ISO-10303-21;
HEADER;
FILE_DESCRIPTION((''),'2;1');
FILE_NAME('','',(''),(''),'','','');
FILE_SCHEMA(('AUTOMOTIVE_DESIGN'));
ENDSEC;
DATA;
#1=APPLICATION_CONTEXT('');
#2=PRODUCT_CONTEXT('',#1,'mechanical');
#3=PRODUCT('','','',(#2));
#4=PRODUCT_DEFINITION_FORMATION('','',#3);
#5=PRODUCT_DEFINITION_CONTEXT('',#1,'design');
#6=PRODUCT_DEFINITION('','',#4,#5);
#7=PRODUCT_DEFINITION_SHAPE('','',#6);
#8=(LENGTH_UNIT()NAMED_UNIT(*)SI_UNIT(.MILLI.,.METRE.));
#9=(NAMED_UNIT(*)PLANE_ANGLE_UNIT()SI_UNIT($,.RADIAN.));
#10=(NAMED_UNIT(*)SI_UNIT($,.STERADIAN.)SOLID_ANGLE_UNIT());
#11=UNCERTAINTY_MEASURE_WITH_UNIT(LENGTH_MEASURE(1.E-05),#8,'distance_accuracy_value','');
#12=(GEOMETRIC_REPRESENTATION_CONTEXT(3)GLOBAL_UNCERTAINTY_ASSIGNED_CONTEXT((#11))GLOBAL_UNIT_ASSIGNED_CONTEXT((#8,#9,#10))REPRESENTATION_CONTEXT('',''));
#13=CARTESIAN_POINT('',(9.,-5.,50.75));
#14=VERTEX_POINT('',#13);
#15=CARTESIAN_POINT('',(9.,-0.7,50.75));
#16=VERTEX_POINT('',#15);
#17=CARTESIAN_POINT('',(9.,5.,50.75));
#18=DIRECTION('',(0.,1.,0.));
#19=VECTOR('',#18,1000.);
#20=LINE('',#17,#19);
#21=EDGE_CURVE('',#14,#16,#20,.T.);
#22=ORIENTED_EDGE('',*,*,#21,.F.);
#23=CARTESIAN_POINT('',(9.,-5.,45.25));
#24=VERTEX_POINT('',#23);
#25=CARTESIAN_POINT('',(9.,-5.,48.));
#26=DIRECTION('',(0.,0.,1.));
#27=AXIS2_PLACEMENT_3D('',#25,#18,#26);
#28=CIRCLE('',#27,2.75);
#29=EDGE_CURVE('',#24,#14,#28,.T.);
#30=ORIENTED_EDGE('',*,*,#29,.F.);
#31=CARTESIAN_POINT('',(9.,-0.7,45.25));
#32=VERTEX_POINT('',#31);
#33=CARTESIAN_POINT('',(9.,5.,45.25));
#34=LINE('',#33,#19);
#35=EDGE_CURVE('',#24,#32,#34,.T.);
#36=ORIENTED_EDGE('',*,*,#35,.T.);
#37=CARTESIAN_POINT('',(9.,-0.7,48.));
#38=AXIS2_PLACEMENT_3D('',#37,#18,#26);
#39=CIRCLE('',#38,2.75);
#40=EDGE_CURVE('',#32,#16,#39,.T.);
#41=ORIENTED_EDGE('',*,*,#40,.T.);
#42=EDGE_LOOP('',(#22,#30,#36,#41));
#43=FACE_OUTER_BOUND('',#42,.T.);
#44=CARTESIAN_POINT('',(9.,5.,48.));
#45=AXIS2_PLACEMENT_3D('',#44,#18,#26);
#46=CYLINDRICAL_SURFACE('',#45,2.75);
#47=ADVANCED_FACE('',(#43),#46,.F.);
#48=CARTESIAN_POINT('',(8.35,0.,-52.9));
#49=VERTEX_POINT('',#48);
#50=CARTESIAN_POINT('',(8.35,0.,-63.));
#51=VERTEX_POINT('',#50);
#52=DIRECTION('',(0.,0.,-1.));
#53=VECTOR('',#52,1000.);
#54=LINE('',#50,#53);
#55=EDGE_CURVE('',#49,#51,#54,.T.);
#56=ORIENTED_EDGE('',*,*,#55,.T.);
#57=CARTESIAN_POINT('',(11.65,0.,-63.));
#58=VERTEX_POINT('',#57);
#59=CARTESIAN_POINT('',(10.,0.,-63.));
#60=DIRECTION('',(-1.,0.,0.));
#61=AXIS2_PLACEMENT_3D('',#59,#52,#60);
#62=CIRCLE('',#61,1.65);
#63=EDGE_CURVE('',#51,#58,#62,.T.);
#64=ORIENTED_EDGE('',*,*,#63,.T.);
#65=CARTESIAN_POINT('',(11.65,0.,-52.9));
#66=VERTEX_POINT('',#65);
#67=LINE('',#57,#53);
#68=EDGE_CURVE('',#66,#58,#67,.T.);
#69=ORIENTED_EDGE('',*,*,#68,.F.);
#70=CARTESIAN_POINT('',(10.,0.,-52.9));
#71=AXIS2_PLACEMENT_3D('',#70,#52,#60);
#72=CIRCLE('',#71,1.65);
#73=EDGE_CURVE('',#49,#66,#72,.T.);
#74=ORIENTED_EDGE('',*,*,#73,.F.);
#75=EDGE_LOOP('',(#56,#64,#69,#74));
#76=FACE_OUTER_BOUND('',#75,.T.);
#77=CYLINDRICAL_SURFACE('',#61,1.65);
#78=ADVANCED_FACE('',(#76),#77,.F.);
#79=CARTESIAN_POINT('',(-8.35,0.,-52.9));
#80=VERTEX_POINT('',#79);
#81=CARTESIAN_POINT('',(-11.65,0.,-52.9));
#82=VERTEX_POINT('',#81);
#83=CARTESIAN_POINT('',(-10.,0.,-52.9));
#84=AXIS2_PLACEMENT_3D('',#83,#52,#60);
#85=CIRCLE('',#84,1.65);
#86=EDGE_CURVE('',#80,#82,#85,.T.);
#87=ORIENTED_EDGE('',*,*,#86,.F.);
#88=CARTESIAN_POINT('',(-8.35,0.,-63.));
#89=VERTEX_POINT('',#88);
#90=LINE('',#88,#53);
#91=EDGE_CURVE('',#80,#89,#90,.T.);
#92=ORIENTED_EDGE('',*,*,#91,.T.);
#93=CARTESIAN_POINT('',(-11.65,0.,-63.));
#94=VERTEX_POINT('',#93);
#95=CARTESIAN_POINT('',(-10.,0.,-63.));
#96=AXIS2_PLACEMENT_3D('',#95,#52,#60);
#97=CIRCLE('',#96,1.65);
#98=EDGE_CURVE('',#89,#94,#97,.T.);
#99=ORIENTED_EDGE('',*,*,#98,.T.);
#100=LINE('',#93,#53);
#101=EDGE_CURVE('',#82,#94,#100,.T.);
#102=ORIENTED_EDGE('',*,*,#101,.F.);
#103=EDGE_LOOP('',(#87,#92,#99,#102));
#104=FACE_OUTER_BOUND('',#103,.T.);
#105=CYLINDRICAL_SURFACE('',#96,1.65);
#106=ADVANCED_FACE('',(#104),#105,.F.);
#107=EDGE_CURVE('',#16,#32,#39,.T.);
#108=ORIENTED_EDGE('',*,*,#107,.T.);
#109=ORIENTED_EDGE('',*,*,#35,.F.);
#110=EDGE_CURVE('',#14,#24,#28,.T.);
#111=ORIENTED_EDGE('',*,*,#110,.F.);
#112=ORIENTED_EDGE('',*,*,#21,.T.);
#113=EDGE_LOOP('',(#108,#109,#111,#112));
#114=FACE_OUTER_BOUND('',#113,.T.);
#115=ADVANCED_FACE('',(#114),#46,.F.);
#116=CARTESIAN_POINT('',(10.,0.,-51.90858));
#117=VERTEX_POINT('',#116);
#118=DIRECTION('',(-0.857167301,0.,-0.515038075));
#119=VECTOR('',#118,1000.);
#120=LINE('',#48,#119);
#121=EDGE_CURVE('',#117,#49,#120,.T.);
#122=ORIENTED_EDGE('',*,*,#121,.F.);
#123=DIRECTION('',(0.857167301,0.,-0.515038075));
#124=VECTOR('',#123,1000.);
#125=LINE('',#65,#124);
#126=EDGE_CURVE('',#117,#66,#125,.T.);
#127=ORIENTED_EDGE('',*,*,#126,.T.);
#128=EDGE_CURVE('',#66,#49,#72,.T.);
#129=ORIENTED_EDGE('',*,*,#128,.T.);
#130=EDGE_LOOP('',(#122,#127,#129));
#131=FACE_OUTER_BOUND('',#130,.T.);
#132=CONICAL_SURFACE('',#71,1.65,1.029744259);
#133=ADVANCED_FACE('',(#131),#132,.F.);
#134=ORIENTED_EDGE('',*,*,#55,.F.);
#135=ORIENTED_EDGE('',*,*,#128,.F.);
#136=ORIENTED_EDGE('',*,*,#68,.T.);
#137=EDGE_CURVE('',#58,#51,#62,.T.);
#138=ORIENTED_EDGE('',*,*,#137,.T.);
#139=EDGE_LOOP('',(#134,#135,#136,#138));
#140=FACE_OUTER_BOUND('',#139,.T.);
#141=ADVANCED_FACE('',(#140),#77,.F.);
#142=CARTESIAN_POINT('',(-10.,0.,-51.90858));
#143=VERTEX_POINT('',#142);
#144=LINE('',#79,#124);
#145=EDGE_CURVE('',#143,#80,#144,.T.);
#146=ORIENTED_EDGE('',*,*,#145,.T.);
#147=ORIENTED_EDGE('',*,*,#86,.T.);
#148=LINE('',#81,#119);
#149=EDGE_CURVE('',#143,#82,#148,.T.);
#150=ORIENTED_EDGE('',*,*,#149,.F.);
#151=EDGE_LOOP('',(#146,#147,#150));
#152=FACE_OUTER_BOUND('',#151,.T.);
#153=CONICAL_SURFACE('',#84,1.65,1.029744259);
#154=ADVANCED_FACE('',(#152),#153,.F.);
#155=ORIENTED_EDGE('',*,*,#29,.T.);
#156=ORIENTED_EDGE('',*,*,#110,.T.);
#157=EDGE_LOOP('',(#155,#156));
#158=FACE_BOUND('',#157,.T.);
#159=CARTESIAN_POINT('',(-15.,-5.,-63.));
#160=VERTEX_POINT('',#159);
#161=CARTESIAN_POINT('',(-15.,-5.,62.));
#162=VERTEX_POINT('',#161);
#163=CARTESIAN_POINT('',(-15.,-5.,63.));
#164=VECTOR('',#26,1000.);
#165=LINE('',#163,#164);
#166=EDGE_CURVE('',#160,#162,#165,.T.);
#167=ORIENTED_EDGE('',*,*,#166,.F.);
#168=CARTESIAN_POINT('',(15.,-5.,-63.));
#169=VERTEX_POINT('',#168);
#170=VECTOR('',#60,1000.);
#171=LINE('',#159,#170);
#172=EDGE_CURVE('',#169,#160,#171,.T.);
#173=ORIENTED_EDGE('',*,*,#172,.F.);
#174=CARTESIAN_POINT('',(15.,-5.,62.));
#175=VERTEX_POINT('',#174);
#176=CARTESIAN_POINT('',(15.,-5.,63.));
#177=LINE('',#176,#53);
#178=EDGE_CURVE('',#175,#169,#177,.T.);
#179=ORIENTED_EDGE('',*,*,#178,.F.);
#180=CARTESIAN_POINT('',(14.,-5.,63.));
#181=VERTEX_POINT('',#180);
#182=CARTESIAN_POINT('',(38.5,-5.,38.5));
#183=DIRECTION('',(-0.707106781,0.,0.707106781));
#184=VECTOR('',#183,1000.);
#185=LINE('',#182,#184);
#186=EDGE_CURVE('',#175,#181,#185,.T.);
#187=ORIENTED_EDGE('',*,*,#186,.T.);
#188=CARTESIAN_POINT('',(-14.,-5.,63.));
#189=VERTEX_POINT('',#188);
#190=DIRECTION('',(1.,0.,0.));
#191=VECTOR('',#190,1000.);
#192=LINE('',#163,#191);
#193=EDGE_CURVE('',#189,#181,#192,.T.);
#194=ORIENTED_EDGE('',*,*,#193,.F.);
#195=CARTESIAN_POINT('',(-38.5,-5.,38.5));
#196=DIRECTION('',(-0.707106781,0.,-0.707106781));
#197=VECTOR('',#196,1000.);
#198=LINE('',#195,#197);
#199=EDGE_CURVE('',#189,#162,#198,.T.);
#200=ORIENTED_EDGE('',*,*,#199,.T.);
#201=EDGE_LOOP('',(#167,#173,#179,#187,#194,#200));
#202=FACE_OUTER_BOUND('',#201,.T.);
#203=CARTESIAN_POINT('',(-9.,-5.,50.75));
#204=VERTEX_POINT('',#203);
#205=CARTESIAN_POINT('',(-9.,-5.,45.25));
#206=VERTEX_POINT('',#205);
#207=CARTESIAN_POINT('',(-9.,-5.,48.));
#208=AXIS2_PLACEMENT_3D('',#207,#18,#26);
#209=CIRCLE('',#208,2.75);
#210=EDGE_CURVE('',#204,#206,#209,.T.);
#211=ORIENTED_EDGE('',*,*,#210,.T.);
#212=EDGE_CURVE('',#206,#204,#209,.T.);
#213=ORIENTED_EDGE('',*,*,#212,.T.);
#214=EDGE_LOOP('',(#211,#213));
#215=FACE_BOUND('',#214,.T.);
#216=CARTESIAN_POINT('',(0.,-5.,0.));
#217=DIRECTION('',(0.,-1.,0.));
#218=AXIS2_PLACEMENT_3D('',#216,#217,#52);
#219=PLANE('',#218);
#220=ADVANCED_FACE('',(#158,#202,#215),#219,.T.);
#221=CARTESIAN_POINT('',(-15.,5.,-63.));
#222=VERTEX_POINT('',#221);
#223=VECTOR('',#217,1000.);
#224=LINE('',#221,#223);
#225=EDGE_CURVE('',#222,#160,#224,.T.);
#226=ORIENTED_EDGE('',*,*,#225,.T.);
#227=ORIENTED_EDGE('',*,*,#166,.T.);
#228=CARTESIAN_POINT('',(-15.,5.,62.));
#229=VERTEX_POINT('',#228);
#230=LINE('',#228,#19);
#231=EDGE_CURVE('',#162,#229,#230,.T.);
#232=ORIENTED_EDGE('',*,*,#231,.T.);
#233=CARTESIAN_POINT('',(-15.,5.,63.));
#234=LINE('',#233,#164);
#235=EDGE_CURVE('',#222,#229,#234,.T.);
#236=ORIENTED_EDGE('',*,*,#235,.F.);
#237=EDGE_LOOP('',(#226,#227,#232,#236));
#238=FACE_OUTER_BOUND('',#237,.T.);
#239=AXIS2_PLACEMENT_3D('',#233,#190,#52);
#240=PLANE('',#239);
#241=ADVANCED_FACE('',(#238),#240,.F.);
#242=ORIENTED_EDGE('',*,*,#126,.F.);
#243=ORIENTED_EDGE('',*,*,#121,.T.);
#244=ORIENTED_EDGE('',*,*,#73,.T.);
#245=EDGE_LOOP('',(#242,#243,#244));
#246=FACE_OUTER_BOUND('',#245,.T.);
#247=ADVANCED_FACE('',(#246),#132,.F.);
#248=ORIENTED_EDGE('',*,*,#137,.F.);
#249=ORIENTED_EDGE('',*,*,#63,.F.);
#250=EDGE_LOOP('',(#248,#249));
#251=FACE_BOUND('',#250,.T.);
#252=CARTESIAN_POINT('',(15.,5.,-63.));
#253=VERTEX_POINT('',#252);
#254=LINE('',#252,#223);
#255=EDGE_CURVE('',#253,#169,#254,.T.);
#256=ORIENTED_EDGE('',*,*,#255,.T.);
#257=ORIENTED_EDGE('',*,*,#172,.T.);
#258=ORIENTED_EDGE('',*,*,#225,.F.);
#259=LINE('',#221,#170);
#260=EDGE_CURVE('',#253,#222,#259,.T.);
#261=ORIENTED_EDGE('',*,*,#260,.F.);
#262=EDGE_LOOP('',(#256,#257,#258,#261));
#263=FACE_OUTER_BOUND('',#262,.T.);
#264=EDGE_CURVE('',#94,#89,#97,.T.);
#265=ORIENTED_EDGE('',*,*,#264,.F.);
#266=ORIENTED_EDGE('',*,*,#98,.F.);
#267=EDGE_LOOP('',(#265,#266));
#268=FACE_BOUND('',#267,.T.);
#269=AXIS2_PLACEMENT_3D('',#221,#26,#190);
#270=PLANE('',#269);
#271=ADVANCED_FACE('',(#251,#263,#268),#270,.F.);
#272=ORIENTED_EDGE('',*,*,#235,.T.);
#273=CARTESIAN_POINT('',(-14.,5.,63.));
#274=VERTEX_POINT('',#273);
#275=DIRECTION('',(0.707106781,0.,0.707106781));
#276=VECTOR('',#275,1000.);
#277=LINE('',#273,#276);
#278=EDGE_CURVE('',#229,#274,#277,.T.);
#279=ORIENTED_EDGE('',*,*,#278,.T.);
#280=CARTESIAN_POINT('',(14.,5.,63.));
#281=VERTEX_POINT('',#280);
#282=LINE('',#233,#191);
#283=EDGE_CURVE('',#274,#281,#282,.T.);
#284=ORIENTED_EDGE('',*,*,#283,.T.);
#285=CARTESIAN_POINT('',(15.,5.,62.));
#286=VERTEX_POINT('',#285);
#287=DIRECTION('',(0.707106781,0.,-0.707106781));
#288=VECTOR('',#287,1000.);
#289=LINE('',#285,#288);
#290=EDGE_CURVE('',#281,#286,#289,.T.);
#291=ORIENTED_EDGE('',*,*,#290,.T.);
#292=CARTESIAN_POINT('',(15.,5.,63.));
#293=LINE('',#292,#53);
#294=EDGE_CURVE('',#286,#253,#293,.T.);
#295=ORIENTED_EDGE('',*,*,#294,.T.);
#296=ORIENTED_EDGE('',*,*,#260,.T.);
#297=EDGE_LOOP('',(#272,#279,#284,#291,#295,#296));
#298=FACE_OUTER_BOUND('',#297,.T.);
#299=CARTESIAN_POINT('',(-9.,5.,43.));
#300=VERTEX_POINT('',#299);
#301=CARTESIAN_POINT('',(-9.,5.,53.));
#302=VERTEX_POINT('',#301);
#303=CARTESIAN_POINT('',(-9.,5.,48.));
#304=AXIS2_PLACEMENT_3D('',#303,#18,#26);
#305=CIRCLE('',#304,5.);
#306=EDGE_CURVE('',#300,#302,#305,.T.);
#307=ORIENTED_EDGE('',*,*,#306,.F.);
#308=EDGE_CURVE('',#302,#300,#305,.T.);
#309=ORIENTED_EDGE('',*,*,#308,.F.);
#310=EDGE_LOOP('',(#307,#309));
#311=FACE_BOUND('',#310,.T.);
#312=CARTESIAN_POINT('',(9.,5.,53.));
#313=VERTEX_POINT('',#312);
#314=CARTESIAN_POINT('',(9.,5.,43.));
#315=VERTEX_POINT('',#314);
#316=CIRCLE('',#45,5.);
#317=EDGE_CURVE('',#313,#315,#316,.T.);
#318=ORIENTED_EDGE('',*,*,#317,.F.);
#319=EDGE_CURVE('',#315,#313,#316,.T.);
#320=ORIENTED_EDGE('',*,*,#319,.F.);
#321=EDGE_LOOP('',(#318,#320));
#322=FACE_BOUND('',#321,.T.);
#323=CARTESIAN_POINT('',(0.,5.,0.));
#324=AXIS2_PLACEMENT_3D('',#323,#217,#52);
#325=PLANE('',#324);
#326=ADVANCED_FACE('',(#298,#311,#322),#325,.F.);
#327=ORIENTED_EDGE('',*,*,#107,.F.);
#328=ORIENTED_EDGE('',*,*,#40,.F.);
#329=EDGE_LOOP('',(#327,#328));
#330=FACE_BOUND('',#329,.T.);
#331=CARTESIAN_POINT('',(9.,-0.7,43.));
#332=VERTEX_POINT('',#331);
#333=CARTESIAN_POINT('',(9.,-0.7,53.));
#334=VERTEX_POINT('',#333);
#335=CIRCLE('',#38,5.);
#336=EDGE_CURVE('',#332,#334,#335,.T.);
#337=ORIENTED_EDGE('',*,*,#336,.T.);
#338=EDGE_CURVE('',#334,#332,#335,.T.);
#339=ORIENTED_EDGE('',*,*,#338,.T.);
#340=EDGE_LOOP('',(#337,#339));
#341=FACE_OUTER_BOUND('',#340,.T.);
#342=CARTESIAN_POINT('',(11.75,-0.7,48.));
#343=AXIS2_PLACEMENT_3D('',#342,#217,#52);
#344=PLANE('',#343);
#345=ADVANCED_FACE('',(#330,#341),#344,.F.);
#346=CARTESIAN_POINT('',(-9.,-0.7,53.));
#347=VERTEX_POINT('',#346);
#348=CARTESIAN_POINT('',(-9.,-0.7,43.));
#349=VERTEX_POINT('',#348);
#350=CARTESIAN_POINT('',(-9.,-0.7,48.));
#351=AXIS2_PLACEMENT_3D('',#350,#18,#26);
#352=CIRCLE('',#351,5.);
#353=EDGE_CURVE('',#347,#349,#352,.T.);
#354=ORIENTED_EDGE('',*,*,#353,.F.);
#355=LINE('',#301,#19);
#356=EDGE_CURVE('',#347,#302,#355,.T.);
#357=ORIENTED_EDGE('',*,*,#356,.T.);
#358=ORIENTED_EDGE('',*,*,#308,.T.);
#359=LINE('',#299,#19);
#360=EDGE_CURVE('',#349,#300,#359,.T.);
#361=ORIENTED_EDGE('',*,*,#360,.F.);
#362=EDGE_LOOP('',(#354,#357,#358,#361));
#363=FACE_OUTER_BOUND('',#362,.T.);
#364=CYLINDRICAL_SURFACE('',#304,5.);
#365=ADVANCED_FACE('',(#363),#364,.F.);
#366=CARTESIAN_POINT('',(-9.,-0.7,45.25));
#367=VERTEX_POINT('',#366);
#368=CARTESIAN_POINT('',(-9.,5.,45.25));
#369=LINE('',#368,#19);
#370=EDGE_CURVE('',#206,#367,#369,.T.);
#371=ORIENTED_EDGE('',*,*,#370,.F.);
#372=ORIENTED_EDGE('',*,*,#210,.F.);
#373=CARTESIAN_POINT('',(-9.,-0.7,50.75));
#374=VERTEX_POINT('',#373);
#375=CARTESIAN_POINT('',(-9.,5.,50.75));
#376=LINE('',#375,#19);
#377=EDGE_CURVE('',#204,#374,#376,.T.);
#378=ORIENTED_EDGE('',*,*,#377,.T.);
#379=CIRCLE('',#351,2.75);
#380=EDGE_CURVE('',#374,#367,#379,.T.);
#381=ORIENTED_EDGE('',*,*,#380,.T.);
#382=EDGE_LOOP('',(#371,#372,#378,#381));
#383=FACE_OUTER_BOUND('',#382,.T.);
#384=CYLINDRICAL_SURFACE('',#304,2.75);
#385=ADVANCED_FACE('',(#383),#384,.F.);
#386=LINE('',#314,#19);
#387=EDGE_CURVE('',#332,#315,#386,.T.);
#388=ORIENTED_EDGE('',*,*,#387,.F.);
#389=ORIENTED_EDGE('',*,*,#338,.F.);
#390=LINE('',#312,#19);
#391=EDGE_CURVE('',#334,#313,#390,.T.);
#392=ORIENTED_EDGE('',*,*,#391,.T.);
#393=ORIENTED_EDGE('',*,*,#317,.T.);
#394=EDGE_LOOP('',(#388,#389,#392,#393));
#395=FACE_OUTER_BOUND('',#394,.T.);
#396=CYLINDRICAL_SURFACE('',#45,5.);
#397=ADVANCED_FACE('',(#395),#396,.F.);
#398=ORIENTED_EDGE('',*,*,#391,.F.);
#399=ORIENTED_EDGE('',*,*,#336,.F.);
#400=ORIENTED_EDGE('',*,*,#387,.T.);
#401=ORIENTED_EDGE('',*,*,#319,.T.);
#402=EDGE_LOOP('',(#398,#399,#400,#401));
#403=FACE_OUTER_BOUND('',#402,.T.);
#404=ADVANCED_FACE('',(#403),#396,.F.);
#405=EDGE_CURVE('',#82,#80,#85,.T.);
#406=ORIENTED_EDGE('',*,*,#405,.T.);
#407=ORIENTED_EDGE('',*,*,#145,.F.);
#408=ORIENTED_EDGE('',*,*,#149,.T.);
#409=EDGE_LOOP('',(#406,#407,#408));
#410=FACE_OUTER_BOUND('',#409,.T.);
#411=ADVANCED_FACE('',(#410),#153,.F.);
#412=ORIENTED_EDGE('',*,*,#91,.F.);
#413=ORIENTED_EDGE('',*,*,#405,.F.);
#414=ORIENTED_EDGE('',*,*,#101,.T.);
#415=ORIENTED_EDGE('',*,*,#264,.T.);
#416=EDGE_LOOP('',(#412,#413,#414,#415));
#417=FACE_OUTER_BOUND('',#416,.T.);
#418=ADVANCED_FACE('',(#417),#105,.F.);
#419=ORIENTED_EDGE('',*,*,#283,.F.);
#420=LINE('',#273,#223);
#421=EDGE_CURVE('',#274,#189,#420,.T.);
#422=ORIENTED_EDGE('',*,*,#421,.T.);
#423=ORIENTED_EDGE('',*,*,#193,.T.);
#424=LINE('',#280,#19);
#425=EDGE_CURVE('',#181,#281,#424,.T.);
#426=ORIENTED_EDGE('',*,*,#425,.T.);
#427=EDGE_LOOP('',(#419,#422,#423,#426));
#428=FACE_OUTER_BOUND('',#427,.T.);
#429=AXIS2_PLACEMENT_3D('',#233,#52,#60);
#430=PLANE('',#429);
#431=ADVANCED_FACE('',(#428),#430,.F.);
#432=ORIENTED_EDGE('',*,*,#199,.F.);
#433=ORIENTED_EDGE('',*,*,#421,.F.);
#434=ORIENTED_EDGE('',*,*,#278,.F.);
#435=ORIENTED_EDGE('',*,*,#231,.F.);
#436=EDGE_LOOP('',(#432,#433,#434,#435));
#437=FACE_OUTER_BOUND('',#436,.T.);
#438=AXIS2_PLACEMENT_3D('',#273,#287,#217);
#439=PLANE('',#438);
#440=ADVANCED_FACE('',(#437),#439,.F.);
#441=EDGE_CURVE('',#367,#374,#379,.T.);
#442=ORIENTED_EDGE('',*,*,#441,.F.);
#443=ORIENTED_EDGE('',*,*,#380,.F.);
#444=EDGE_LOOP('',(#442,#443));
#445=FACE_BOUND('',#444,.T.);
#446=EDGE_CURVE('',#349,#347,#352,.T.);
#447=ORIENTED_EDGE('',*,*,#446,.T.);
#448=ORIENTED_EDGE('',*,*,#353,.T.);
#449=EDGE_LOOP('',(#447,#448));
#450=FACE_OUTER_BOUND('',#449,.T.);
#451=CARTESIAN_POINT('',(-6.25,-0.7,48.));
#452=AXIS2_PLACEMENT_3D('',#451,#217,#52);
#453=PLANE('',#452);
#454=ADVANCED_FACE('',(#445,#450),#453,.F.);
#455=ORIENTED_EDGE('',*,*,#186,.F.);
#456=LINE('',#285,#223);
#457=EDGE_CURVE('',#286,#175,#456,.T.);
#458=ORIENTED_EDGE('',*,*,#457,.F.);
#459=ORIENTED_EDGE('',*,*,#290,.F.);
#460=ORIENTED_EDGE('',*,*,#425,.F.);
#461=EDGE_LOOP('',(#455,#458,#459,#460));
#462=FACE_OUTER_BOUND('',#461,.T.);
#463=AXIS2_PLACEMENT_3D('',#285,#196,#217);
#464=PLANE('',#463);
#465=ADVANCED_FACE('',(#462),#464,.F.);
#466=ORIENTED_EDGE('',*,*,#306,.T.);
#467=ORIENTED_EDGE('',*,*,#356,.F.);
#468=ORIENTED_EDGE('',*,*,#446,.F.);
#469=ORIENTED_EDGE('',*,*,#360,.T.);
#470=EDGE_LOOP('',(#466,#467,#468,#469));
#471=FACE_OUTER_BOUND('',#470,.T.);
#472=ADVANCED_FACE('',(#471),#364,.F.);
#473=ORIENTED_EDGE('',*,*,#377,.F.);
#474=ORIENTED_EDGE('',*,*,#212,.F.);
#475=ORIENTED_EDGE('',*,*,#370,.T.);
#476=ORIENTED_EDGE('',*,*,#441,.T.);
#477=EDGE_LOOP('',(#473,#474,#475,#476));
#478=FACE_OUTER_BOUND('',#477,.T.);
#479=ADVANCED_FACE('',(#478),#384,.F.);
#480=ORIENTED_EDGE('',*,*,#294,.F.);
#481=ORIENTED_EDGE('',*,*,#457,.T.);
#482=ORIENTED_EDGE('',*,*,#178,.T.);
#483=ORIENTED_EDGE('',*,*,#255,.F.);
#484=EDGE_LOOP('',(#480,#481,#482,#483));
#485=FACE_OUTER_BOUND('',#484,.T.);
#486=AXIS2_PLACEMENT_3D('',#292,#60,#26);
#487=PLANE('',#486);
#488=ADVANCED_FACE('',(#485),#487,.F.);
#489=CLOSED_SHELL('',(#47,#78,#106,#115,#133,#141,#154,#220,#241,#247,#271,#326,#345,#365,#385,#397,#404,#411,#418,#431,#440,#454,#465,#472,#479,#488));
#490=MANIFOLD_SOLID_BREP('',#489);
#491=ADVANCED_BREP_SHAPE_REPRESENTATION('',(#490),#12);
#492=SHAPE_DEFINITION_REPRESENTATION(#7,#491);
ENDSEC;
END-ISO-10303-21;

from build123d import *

# Parameters (mm, degrees)
SKETCH_1_W                = 30
SKETCH_1_H                = 126
EXTRUDE_1_DEPTH           = 5
HOLE_WIZARD_1_D           = 5.5
HOLE_WIZARD_1_CBORE_D     = 10
HOLE_WIZARD_1_CBORE_DEPTH = 5.7
CHAMFER_1_SIZE            = 1
HOLE_WIZARD_M4_1_D        = 3.3
HOLE_WIZARD_M4_1_DEPTH    = 10.1
HOLE_WIZARD_M4_1_TIP      = 0.991420021


with BuildPart() as part:
    # 草图1 → 凸台-拉伸1 (new, symmetric)
    with BuildSketch(Plane(origin=(0, 0, 0), x_dir=(1, 0, 0), z_dir=(0, 1, 0))):
        Rectangle(SKETCH_1_W, SKETCH_1_H)
    extrude(amount=EXTRUDE_1_DEPTH, both=True)

    # 打孔尺寸(%根据)内六角圆柱头螺钉的类型1 (through all)
    with Locations(Plane(origin=(0, 5, 0), x_dir=(1, 0, 0), z_dir=(0, 1, 0))):
        with Locations((9, -48), (-9, -48)):
            CounterBoreHole(HOLE_WIZARD_1_D / 2, HOLE_WIZARD_1_CBORE_D / 2, HOLE_WIZARD_1_CBORE_DEPTH)

    # 倒角1
    chamfer_1_edges = [part.edges().sort_by_distance(p)[0] for p in [
        (15, 0, 63),
        (-15, 0, 63),
    ]]
    chamfer(chamfer_1_edges, length=CHAMFER_1_SIZE)

    # M4 螺纹孔1
    with Locations(Plane(origin=(0, 0, -63), x_dir=(-1, 0, 0), z_dir=(0, 0, -1))):
        with Locations((-10, 0), (10, 0)):
            Hole(HOLE_WIZARD_M4_1_D / 2, depth=HOLE_WIZARD_M4_1_DEPTH)
            with Locations((0, 0, -(HOLE_WIZARD_M4_1_DEPTH + HOLE_WIZARD_M4_1_TIP / 2))):  # 118° drill point
                Cone(0, HOLE_WIZARD_M4_1_D / 2, HOLE_WIZARD_M4_1_TIP, mode=Mode.SUBTRACT)


solid = part.part
